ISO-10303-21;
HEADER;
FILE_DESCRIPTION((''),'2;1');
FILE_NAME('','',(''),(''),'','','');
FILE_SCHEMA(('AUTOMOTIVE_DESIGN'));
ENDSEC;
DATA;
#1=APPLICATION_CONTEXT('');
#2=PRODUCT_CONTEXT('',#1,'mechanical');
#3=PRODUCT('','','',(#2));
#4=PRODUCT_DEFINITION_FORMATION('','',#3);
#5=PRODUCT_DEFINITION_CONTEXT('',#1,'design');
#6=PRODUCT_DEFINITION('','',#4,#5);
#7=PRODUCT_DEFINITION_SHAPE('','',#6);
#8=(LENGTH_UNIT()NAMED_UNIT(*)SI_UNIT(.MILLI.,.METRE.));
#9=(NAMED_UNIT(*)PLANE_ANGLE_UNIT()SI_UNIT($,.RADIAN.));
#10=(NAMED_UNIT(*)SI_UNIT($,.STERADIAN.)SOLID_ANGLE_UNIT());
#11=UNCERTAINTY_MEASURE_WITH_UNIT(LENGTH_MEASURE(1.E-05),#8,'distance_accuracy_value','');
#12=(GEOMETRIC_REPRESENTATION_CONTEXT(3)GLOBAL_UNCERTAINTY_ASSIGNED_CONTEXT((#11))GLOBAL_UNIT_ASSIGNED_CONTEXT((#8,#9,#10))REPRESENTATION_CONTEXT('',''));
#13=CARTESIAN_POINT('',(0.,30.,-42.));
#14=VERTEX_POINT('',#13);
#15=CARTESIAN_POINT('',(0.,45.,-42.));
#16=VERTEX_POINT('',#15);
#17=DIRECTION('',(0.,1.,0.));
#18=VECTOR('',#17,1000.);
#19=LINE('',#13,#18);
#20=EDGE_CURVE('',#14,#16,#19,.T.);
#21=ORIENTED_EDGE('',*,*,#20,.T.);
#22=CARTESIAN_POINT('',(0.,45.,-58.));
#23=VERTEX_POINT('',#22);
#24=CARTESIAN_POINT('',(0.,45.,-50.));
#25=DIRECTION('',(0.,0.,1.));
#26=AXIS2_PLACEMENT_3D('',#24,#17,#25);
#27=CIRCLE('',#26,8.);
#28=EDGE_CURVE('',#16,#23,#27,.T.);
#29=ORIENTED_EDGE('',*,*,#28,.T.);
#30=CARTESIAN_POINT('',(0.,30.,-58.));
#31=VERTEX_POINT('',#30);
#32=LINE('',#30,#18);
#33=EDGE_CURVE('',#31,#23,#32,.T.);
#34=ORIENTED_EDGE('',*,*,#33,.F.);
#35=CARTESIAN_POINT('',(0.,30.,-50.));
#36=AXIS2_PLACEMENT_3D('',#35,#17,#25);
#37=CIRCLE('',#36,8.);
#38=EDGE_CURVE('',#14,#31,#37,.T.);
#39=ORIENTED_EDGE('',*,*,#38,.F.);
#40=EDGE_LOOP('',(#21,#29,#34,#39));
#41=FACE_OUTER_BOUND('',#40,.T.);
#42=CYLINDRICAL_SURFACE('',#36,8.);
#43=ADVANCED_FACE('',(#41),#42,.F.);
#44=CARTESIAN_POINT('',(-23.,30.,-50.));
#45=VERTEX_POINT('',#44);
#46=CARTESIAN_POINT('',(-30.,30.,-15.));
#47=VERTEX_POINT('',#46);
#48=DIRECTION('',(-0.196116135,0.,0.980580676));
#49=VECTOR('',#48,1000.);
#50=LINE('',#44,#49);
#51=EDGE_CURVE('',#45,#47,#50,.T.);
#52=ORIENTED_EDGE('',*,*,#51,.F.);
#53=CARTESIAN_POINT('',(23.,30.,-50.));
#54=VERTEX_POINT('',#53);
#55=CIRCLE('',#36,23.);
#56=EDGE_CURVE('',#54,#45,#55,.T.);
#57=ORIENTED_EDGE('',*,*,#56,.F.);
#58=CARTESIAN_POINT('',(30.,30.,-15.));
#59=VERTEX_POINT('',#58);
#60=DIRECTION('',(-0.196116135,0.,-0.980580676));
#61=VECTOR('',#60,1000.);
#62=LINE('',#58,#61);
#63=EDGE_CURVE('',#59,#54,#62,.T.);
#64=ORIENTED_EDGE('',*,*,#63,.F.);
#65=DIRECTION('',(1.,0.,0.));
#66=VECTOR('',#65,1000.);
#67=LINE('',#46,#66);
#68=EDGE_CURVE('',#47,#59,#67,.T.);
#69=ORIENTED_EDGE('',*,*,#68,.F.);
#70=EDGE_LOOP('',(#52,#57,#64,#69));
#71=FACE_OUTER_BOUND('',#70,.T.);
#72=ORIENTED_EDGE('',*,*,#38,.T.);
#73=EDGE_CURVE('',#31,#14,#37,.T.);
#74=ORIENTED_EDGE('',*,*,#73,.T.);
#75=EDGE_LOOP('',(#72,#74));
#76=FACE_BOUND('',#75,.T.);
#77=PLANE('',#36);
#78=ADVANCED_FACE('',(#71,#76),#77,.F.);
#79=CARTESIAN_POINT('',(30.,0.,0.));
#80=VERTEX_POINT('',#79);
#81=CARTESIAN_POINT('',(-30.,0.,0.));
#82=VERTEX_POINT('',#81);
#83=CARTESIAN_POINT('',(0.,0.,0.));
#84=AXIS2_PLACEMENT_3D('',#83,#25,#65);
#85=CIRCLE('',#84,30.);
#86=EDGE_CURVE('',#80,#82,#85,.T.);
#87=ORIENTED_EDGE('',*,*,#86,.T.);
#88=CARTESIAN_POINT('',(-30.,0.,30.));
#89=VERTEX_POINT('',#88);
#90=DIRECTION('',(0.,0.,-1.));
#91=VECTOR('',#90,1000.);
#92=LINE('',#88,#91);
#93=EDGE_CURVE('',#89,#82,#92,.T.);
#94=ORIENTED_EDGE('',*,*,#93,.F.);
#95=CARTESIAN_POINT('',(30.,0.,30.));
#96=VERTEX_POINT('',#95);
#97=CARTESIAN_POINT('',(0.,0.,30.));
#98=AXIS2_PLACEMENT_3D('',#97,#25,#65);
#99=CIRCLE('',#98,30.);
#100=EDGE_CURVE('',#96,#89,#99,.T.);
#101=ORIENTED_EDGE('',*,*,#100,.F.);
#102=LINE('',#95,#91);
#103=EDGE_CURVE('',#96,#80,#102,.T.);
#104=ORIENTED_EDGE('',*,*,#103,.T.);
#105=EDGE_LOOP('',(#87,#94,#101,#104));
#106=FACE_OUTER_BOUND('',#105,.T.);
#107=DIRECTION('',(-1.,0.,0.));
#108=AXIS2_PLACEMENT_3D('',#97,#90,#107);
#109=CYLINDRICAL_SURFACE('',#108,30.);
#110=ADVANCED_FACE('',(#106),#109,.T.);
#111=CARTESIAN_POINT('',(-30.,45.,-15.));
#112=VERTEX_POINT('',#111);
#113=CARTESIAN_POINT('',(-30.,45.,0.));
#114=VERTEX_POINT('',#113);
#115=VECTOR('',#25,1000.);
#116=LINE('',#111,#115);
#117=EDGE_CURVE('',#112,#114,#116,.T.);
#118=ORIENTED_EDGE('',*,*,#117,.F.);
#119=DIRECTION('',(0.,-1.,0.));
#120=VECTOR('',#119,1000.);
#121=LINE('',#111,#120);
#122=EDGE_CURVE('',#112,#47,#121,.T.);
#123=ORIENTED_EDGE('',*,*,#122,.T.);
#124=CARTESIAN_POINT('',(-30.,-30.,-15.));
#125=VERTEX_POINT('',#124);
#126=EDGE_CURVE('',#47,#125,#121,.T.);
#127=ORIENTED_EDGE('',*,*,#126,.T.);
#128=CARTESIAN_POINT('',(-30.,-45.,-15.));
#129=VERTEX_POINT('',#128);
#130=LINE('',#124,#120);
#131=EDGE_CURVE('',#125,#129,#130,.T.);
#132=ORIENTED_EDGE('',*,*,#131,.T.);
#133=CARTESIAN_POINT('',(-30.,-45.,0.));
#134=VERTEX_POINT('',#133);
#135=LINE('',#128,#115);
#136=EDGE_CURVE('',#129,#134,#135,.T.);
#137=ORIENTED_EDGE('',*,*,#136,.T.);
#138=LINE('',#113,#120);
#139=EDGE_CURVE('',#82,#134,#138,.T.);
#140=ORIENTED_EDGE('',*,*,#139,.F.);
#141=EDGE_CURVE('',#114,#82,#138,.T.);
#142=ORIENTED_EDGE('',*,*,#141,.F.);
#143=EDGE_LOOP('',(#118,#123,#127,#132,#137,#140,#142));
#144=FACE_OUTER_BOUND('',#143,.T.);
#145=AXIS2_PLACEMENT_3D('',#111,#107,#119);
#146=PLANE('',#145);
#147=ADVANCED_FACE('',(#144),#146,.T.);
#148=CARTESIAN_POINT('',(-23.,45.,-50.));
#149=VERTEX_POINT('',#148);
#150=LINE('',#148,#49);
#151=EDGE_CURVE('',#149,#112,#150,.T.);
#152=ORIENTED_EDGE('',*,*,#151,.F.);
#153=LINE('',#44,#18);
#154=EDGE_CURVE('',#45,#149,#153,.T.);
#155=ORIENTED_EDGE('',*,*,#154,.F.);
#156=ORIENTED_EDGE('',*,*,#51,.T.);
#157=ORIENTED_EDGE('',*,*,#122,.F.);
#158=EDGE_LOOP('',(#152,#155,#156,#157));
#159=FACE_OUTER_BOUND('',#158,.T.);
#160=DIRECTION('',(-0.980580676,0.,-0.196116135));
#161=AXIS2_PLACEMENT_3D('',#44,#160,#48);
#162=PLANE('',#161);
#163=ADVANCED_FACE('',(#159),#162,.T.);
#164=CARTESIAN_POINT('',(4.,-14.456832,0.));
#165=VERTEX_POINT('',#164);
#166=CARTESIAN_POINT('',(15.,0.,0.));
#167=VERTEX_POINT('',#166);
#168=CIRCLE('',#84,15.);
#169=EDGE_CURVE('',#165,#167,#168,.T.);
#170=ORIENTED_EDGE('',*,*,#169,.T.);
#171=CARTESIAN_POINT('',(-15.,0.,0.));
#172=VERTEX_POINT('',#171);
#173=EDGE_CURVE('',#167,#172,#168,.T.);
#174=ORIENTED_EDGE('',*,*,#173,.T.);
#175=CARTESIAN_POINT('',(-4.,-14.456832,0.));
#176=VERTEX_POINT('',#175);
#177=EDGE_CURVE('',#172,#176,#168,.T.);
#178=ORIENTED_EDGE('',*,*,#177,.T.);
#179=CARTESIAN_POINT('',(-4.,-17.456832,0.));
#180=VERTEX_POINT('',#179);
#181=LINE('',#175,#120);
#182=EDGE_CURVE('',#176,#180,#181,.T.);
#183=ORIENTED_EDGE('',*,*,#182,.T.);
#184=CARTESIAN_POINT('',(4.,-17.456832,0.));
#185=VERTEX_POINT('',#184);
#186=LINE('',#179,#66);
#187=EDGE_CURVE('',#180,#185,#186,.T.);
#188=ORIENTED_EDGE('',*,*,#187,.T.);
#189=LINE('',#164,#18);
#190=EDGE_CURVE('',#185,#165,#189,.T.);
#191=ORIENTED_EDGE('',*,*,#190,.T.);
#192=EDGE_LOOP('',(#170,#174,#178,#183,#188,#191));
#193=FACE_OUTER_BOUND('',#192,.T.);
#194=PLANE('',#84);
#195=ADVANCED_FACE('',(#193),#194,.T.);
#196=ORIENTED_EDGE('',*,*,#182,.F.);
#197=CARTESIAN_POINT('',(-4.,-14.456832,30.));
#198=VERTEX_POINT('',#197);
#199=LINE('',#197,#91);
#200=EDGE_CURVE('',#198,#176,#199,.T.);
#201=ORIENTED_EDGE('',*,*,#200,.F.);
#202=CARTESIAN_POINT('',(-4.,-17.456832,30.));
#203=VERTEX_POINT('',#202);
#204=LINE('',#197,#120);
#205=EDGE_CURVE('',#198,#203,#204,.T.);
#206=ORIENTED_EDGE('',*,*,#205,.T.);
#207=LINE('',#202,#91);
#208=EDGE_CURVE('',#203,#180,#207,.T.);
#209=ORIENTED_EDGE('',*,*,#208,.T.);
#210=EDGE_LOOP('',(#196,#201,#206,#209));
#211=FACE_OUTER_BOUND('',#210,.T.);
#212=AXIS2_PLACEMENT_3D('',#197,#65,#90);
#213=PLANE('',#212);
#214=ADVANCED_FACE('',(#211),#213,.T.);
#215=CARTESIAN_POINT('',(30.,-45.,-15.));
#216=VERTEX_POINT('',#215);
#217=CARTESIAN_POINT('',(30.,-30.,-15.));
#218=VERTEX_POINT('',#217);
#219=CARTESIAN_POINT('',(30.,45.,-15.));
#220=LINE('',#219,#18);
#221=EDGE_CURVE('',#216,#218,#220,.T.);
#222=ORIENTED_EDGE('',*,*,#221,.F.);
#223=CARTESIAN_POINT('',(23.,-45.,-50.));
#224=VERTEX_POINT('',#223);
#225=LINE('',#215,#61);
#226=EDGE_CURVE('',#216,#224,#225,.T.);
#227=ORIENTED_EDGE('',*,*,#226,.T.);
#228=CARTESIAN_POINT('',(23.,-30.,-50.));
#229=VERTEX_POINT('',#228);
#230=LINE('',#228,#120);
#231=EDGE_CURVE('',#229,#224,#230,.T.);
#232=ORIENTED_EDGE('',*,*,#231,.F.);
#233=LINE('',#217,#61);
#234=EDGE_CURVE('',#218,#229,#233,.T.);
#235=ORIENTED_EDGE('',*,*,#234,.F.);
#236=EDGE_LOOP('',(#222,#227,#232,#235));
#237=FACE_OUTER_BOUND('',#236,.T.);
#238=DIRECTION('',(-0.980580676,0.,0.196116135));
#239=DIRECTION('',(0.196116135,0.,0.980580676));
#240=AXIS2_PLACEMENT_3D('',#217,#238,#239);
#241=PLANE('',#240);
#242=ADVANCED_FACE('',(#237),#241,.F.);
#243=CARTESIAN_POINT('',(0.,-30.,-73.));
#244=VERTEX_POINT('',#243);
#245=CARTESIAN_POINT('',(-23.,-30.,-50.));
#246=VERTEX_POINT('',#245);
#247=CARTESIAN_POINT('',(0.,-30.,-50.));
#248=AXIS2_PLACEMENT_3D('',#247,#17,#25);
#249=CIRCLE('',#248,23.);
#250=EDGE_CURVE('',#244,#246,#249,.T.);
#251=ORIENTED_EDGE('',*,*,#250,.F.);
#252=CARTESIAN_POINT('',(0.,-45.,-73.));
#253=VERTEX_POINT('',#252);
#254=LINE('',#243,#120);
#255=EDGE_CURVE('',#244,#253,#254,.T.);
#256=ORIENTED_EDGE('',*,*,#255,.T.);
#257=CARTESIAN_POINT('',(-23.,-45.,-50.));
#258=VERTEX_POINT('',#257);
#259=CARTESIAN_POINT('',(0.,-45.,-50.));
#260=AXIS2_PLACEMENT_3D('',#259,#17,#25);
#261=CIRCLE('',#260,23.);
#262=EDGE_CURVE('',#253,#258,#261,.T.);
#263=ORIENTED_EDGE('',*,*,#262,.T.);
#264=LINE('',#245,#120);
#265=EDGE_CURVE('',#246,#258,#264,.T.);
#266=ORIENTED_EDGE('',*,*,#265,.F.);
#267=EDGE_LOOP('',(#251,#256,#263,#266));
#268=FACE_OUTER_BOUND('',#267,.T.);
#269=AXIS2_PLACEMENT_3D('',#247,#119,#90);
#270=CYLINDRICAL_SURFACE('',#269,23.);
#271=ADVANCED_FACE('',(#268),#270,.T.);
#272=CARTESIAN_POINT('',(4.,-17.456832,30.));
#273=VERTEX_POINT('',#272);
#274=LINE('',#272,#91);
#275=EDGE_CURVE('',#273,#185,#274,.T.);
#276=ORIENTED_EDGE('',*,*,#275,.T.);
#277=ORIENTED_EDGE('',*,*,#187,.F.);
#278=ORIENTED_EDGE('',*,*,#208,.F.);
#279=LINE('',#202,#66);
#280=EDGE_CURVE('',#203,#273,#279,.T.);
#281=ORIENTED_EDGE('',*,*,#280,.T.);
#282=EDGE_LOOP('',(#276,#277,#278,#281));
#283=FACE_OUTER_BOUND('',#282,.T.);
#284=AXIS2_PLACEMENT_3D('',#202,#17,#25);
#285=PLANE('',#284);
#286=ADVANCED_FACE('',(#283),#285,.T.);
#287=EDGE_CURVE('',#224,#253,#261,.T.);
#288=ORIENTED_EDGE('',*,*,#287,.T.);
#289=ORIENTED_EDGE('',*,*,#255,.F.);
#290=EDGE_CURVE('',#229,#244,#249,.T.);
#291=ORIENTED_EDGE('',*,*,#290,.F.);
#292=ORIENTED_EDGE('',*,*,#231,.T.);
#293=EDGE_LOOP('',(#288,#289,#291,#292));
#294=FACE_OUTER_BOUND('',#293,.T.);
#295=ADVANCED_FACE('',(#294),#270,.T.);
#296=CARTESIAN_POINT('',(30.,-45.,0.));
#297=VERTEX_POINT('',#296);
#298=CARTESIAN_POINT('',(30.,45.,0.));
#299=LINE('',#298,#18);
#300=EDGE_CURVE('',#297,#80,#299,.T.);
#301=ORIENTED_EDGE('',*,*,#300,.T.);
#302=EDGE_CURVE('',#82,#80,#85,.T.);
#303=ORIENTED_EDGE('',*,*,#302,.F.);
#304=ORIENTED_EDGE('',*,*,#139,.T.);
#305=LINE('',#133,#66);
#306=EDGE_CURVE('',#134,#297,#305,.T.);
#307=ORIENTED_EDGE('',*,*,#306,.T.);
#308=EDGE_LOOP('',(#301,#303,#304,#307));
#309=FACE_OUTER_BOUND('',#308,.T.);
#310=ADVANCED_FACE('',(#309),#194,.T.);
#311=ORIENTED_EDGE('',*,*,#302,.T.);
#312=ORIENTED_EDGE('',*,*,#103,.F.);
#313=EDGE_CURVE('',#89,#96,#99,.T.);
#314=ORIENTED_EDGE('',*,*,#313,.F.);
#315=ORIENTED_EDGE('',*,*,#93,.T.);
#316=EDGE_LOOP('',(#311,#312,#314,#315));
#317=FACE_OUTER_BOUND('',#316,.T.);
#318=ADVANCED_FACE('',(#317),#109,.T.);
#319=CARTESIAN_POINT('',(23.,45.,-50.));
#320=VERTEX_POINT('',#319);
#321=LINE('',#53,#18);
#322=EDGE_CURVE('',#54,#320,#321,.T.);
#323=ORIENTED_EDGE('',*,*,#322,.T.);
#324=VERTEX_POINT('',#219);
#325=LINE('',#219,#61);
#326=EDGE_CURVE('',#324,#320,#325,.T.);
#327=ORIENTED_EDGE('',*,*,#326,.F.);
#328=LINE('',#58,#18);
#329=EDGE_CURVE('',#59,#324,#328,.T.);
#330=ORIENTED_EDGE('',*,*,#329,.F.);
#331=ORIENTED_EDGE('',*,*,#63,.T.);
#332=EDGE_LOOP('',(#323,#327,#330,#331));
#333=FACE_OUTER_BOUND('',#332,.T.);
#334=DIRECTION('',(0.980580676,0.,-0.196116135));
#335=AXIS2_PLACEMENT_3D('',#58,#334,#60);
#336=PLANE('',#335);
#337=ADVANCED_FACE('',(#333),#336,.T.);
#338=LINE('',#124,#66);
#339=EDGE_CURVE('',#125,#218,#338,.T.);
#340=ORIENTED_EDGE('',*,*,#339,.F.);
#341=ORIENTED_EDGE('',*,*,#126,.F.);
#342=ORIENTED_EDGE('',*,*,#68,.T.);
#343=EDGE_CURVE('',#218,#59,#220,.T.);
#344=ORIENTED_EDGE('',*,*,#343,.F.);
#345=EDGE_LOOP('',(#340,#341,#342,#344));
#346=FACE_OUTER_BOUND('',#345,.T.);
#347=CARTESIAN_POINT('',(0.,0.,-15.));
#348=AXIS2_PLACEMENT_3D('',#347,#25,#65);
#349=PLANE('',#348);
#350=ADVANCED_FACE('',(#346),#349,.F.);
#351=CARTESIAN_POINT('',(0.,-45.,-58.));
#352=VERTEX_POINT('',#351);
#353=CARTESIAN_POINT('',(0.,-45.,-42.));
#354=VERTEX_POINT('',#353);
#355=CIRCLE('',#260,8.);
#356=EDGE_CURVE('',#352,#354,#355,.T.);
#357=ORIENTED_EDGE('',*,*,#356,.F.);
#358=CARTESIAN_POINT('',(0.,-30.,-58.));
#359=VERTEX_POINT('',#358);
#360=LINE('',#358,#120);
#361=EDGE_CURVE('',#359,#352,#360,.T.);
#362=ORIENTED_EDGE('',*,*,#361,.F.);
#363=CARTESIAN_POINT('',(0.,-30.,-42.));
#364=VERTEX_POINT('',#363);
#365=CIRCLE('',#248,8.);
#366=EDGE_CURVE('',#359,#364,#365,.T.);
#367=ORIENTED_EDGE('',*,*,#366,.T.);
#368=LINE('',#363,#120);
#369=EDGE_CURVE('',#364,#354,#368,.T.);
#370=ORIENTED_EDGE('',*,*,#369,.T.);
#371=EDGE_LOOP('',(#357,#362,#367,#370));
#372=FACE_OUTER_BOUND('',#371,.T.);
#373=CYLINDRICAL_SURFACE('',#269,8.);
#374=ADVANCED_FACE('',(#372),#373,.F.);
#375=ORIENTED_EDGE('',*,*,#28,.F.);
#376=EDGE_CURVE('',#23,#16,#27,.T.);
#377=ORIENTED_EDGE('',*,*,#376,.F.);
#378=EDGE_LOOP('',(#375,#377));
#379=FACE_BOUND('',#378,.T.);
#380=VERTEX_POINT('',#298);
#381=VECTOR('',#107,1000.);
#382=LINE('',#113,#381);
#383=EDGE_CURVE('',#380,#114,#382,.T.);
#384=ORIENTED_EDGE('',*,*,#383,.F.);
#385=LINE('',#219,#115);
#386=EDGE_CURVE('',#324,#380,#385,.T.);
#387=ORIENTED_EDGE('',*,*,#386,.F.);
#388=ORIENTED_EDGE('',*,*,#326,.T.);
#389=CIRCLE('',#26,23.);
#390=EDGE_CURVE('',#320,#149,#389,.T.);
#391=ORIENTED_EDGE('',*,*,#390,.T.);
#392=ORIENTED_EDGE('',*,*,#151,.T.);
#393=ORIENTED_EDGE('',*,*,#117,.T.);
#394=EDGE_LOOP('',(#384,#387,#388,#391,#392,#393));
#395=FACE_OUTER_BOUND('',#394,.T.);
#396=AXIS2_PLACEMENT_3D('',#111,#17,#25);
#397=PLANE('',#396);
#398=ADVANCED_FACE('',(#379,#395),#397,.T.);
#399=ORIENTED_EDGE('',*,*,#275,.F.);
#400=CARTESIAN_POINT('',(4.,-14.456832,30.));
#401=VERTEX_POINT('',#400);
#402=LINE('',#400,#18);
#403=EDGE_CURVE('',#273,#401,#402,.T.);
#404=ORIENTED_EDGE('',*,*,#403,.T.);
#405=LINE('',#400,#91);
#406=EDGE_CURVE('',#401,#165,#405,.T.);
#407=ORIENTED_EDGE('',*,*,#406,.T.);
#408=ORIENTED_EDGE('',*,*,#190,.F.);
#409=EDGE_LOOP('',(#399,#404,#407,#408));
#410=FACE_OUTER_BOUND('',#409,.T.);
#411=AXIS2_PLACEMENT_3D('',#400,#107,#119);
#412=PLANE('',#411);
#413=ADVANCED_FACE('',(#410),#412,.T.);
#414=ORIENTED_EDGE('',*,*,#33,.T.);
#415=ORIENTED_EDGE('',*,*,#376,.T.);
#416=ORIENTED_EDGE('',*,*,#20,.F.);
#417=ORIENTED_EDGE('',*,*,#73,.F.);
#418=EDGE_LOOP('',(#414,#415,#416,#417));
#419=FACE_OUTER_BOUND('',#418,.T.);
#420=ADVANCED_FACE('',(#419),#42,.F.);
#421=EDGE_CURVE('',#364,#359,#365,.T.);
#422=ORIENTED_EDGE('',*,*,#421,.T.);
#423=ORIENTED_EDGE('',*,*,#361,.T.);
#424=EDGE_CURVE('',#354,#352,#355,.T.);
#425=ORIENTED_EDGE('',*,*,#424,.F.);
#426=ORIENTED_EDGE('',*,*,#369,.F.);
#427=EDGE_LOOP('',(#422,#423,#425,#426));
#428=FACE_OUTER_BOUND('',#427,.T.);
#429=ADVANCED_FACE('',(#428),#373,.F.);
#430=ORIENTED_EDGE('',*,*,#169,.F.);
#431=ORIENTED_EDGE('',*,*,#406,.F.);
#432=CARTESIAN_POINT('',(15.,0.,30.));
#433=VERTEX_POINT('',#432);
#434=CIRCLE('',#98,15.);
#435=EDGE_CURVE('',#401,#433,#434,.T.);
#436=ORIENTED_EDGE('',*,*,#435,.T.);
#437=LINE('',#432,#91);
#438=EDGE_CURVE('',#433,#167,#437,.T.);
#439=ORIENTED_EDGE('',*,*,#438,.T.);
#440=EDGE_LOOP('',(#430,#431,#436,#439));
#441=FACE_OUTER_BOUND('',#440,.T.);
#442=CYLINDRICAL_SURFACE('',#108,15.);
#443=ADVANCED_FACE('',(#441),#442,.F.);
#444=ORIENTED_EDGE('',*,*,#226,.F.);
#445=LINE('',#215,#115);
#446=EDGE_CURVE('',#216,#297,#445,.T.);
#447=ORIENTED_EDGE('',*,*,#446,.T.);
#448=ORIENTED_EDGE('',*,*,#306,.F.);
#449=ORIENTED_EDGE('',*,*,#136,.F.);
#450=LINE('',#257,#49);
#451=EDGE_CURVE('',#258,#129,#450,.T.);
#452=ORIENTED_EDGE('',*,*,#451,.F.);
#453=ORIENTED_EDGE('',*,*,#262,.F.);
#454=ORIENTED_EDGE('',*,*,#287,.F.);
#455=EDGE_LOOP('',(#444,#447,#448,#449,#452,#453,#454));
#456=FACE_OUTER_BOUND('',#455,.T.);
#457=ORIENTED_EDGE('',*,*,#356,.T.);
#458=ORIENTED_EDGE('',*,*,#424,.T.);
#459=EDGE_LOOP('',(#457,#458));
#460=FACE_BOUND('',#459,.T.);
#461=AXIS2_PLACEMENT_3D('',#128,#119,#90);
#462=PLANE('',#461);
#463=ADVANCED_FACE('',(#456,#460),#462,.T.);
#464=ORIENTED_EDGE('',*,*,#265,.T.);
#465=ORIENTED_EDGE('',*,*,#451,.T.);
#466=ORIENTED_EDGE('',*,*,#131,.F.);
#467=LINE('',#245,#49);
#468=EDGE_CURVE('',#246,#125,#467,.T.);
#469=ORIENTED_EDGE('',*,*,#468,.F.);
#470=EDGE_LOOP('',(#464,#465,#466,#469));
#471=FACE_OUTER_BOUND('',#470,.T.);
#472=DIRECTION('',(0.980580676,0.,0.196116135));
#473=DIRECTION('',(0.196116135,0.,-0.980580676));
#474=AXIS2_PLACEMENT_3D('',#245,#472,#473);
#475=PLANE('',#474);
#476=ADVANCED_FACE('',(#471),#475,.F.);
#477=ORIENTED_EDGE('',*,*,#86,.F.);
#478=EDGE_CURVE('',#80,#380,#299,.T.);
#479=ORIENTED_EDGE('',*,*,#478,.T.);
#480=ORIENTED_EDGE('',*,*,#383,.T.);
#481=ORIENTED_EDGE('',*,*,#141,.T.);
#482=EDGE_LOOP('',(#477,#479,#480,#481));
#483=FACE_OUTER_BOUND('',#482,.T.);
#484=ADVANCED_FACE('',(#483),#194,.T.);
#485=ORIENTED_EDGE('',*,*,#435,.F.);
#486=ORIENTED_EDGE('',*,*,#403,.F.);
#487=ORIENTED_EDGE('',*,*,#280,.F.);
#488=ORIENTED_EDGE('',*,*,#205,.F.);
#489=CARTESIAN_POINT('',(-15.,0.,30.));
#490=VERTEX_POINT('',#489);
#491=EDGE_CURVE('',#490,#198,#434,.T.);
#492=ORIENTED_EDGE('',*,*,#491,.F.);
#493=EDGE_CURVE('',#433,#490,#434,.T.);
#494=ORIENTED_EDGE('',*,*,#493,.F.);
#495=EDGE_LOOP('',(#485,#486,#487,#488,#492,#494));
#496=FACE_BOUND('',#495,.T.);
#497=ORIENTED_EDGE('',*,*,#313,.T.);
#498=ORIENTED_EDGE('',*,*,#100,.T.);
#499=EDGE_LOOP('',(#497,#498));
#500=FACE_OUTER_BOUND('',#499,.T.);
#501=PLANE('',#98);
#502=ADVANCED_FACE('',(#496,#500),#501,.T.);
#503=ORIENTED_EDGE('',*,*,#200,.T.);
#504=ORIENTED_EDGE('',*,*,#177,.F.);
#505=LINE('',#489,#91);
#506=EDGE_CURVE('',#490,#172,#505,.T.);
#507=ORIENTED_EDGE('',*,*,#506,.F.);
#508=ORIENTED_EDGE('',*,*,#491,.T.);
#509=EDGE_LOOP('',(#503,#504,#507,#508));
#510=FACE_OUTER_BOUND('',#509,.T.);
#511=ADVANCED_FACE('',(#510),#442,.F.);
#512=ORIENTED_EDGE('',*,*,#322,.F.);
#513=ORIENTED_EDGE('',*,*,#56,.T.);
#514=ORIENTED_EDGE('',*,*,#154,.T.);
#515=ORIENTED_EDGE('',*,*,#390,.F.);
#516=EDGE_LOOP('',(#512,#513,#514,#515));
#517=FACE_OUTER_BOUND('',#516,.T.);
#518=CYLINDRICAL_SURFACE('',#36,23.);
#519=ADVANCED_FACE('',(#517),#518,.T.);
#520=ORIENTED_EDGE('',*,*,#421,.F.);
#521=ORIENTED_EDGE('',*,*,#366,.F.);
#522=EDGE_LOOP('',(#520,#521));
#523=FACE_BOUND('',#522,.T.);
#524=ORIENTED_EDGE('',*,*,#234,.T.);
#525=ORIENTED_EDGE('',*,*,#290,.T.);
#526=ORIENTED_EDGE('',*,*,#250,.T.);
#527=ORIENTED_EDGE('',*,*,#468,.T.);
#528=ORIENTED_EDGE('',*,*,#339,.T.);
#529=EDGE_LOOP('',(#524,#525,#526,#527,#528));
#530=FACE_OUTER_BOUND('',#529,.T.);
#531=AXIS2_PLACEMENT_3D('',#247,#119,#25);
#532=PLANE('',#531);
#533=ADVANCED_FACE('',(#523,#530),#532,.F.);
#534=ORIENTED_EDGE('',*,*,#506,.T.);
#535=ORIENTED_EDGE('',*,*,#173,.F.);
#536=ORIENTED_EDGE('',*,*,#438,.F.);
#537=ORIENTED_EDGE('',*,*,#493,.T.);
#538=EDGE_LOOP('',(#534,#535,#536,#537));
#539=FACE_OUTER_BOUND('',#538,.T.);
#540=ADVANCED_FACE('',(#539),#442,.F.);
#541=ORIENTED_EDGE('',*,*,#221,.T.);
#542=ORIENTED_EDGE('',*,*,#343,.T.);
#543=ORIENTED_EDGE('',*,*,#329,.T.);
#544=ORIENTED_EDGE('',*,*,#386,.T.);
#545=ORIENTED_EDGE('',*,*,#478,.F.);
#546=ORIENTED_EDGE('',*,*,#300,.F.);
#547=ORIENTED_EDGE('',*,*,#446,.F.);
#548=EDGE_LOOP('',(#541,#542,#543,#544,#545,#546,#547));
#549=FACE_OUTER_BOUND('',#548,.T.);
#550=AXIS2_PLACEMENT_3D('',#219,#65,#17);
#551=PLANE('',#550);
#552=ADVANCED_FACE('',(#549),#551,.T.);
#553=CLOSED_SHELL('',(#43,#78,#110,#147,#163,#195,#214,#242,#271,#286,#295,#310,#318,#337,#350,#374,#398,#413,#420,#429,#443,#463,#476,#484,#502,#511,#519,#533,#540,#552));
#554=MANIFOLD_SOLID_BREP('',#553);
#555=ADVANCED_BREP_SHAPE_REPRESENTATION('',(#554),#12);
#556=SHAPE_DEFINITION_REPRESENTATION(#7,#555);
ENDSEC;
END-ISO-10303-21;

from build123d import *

# Parameters (mm, degrees)
SKETCH1_W           = 60
SKETCH1_H           = 90
BOSS_EXTRUDE1_DEPTH = 15
SKETCH2_R           = 8
BOSS_EXTRUDE2_DEPTH = 15
SKETCH3_R           = 30
BOSS_EXTRUDE3_DEPTH = 30


with BuildPart() as part:
    # Sketch1 → Boss-Extrude1 (new body)
    with BuildSketch(Plane.XY):
        Rectangle(SKETCH1_W, SKETCH1_H)
    extrude(amount=-BOSS_EXTRUDE1_DEPTH)

    # Sketch2 → Boss-Extrude2 (add)
    with BuildSketch(Plane(origin=(0, 45, 0), x_dir=(1, 0, 0), z_dir=(0, 1, 0))):
        with BuildLine():
            Line((-23, 50), (-30, 15))
            Line((-30, 15), (30, 15))
            Line((30, 15), (23, 50))
            ThreePointArc((23, 50), (0, 73), (-23, 50))
        make_face()
        with Locations(Location((0, 50, 0), (0, 0, 270))):
            Circle(SKETCH2_R, mode=Mode.SUBTRACT)
    boss_extrude2 = extrude(amount=-BOSS_EXTRUDE2_DEPTH)

    # Mirror1: Boss-Extrude2 across plane
    add(boss_extrude2.mirror(Plane.ZX))

    # Sketch3 → Boss-Extrude3 (add)
    with BuildSketch(Plane.XY):
        Circle(SKETCH3_R)
        with BuildLine():
            Line((-4, -14.456832295), (-4, -17.456832295))
            Line((-4, -17.456832295), (4, -17.456832295))
            Line((4, -17.456832295), (4, -14.456832295))
            ThreePointArc((4, -14.456832295), (0, 15), (-4, -14.456832295))
        make_face(mode=Mode.SUBTRACT)
    extrude(amount=BOSS_EXTRUDE3_DEPTH)


solid = part.part
